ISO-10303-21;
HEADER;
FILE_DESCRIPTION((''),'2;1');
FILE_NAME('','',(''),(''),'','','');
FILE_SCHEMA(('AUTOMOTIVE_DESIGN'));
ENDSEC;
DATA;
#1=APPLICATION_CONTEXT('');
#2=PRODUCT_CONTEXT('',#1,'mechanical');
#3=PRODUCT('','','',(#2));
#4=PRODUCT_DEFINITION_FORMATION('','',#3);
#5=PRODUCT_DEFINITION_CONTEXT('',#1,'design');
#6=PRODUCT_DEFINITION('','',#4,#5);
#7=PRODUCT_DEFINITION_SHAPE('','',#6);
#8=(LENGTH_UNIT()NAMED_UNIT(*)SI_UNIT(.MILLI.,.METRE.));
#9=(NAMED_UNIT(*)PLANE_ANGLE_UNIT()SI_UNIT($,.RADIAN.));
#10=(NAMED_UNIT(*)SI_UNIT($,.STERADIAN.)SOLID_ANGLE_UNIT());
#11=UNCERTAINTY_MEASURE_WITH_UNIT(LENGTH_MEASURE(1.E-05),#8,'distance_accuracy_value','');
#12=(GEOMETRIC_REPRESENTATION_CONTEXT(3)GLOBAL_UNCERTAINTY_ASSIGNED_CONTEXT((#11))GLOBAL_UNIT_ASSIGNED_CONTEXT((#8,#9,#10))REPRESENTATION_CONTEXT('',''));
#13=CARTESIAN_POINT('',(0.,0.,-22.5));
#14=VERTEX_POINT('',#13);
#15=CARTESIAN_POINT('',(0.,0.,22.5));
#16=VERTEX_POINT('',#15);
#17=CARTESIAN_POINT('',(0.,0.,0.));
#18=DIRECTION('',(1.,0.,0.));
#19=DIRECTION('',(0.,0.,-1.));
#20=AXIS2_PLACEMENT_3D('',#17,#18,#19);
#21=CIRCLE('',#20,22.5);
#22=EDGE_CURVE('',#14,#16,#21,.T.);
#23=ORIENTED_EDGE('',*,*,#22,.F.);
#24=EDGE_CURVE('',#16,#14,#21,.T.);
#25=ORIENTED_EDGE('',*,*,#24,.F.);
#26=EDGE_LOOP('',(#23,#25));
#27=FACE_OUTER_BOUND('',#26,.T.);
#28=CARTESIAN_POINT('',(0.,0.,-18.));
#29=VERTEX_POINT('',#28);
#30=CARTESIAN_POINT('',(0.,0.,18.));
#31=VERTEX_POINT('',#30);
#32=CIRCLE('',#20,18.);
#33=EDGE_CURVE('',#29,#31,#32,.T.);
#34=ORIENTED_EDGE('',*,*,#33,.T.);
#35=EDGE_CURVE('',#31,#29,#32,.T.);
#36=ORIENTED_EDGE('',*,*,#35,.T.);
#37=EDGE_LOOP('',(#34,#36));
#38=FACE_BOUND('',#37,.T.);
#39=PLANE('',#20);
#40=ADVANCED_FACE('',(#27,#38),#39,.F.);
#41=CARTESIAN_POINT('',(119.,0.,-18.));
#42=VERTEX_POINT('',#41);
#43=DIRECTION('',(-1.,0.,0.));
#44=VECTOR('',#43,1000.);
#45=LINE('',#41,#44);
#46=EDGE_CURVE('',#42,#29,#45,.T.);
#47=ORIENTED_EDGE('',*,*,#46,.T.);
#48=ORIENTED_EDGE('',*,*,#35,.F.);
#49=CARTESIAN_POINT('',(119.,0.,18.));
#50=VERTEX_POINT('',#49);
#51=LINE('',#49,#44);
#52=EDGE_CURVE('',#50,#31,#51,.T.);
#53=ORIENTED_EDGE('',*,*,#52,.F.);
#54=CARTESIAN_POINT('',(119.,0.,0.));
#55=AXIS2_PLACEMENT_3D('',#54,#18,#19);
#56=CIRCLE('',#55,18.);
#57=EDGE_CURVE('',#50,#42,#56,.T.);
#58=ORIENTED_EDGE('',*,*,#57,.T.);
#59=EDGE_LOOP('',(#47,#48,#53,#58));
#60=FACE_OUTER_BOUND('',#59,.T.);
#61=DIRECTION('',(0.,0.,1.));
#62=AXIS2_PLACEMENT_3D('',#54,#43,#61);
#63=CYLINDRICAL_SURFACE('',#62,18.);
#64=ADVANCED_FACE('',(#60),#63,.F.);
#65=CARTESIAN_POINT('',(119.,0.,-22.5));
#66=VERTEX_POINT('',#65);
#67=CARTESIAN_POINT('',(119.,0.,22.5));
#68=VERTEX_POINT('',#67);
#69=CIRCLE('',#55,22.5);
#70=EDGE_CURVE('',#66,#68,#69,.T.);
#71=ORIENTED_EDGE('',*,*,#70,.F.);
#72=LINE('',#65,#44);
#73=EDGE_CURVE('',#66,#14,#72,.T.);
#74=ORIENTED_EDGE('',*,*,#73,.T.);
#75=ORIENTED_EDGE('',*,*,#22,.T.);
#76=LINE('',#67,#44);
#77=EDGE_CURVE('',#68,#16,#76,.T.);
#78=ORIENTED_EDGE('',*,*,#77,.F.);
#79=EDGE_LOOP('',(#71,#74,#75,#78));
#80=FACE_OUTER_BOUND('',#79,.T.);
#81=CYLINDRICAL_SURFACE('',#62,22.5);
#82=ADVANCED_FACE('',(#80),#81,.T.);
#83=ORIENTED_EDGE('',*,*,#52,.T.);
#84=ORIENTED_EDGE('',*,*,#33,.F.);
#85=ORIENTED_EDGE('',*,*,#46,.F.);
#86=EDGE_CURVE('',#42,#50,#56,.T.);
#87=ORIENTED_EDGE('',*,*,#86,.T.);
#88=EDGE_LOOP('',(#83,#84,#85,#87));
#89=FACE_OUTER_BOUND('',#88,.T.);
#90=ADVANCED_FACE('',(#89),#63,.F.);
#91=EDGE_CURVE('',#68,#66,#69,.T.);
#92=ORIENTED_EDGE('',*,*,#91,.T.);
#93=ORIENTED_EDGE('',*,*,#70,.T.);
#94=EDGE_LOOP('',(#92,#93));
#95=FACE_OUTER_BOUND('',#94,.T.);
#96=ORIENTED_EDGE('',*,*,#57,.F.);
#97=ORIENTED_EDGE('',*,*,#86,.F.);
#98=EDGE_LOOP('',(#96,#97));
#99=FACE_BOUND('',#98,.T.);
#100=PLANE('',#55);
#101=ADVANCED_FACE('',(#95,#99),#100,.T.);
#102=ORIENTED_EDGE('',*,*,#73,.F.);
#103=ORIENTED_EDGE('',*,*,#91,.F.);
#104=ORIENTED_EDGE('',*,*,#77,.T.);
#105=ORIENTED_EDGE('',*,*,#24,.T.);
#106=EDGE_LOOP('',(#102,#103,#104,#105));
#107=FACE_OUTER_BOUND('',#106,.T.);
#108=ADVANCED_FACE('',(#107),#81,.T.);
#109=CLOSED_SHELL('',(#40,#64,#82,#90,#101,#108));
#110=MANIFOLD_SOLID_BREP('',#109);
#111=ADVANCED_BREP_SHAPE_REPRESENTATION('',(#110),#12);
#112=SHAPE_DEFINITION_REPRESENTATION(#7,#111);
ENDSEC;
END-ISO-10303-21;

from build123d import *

# Parameters (mm, degrees)
SKETCH_1_R      = 22.5
SKETCH_1_R_2    = 18
EXTRUDE_1_DEPTH = 119


with BuildPart() as part:
    # 草图1 → 凸台-拉伸1 (new body)
    with BuildSketch(Plane(origin=(0, 0, 0), x_dir=(0, 0, -1), z_dir=(1, 0, 0))):
        Circle(SKETCH_1_R)
        Circle(SKETCH_1_R_2, mode=Mode.SUBTRACT)
    extrude(amount=EXTRUDE_1_DEPTH)


solid = part.part
